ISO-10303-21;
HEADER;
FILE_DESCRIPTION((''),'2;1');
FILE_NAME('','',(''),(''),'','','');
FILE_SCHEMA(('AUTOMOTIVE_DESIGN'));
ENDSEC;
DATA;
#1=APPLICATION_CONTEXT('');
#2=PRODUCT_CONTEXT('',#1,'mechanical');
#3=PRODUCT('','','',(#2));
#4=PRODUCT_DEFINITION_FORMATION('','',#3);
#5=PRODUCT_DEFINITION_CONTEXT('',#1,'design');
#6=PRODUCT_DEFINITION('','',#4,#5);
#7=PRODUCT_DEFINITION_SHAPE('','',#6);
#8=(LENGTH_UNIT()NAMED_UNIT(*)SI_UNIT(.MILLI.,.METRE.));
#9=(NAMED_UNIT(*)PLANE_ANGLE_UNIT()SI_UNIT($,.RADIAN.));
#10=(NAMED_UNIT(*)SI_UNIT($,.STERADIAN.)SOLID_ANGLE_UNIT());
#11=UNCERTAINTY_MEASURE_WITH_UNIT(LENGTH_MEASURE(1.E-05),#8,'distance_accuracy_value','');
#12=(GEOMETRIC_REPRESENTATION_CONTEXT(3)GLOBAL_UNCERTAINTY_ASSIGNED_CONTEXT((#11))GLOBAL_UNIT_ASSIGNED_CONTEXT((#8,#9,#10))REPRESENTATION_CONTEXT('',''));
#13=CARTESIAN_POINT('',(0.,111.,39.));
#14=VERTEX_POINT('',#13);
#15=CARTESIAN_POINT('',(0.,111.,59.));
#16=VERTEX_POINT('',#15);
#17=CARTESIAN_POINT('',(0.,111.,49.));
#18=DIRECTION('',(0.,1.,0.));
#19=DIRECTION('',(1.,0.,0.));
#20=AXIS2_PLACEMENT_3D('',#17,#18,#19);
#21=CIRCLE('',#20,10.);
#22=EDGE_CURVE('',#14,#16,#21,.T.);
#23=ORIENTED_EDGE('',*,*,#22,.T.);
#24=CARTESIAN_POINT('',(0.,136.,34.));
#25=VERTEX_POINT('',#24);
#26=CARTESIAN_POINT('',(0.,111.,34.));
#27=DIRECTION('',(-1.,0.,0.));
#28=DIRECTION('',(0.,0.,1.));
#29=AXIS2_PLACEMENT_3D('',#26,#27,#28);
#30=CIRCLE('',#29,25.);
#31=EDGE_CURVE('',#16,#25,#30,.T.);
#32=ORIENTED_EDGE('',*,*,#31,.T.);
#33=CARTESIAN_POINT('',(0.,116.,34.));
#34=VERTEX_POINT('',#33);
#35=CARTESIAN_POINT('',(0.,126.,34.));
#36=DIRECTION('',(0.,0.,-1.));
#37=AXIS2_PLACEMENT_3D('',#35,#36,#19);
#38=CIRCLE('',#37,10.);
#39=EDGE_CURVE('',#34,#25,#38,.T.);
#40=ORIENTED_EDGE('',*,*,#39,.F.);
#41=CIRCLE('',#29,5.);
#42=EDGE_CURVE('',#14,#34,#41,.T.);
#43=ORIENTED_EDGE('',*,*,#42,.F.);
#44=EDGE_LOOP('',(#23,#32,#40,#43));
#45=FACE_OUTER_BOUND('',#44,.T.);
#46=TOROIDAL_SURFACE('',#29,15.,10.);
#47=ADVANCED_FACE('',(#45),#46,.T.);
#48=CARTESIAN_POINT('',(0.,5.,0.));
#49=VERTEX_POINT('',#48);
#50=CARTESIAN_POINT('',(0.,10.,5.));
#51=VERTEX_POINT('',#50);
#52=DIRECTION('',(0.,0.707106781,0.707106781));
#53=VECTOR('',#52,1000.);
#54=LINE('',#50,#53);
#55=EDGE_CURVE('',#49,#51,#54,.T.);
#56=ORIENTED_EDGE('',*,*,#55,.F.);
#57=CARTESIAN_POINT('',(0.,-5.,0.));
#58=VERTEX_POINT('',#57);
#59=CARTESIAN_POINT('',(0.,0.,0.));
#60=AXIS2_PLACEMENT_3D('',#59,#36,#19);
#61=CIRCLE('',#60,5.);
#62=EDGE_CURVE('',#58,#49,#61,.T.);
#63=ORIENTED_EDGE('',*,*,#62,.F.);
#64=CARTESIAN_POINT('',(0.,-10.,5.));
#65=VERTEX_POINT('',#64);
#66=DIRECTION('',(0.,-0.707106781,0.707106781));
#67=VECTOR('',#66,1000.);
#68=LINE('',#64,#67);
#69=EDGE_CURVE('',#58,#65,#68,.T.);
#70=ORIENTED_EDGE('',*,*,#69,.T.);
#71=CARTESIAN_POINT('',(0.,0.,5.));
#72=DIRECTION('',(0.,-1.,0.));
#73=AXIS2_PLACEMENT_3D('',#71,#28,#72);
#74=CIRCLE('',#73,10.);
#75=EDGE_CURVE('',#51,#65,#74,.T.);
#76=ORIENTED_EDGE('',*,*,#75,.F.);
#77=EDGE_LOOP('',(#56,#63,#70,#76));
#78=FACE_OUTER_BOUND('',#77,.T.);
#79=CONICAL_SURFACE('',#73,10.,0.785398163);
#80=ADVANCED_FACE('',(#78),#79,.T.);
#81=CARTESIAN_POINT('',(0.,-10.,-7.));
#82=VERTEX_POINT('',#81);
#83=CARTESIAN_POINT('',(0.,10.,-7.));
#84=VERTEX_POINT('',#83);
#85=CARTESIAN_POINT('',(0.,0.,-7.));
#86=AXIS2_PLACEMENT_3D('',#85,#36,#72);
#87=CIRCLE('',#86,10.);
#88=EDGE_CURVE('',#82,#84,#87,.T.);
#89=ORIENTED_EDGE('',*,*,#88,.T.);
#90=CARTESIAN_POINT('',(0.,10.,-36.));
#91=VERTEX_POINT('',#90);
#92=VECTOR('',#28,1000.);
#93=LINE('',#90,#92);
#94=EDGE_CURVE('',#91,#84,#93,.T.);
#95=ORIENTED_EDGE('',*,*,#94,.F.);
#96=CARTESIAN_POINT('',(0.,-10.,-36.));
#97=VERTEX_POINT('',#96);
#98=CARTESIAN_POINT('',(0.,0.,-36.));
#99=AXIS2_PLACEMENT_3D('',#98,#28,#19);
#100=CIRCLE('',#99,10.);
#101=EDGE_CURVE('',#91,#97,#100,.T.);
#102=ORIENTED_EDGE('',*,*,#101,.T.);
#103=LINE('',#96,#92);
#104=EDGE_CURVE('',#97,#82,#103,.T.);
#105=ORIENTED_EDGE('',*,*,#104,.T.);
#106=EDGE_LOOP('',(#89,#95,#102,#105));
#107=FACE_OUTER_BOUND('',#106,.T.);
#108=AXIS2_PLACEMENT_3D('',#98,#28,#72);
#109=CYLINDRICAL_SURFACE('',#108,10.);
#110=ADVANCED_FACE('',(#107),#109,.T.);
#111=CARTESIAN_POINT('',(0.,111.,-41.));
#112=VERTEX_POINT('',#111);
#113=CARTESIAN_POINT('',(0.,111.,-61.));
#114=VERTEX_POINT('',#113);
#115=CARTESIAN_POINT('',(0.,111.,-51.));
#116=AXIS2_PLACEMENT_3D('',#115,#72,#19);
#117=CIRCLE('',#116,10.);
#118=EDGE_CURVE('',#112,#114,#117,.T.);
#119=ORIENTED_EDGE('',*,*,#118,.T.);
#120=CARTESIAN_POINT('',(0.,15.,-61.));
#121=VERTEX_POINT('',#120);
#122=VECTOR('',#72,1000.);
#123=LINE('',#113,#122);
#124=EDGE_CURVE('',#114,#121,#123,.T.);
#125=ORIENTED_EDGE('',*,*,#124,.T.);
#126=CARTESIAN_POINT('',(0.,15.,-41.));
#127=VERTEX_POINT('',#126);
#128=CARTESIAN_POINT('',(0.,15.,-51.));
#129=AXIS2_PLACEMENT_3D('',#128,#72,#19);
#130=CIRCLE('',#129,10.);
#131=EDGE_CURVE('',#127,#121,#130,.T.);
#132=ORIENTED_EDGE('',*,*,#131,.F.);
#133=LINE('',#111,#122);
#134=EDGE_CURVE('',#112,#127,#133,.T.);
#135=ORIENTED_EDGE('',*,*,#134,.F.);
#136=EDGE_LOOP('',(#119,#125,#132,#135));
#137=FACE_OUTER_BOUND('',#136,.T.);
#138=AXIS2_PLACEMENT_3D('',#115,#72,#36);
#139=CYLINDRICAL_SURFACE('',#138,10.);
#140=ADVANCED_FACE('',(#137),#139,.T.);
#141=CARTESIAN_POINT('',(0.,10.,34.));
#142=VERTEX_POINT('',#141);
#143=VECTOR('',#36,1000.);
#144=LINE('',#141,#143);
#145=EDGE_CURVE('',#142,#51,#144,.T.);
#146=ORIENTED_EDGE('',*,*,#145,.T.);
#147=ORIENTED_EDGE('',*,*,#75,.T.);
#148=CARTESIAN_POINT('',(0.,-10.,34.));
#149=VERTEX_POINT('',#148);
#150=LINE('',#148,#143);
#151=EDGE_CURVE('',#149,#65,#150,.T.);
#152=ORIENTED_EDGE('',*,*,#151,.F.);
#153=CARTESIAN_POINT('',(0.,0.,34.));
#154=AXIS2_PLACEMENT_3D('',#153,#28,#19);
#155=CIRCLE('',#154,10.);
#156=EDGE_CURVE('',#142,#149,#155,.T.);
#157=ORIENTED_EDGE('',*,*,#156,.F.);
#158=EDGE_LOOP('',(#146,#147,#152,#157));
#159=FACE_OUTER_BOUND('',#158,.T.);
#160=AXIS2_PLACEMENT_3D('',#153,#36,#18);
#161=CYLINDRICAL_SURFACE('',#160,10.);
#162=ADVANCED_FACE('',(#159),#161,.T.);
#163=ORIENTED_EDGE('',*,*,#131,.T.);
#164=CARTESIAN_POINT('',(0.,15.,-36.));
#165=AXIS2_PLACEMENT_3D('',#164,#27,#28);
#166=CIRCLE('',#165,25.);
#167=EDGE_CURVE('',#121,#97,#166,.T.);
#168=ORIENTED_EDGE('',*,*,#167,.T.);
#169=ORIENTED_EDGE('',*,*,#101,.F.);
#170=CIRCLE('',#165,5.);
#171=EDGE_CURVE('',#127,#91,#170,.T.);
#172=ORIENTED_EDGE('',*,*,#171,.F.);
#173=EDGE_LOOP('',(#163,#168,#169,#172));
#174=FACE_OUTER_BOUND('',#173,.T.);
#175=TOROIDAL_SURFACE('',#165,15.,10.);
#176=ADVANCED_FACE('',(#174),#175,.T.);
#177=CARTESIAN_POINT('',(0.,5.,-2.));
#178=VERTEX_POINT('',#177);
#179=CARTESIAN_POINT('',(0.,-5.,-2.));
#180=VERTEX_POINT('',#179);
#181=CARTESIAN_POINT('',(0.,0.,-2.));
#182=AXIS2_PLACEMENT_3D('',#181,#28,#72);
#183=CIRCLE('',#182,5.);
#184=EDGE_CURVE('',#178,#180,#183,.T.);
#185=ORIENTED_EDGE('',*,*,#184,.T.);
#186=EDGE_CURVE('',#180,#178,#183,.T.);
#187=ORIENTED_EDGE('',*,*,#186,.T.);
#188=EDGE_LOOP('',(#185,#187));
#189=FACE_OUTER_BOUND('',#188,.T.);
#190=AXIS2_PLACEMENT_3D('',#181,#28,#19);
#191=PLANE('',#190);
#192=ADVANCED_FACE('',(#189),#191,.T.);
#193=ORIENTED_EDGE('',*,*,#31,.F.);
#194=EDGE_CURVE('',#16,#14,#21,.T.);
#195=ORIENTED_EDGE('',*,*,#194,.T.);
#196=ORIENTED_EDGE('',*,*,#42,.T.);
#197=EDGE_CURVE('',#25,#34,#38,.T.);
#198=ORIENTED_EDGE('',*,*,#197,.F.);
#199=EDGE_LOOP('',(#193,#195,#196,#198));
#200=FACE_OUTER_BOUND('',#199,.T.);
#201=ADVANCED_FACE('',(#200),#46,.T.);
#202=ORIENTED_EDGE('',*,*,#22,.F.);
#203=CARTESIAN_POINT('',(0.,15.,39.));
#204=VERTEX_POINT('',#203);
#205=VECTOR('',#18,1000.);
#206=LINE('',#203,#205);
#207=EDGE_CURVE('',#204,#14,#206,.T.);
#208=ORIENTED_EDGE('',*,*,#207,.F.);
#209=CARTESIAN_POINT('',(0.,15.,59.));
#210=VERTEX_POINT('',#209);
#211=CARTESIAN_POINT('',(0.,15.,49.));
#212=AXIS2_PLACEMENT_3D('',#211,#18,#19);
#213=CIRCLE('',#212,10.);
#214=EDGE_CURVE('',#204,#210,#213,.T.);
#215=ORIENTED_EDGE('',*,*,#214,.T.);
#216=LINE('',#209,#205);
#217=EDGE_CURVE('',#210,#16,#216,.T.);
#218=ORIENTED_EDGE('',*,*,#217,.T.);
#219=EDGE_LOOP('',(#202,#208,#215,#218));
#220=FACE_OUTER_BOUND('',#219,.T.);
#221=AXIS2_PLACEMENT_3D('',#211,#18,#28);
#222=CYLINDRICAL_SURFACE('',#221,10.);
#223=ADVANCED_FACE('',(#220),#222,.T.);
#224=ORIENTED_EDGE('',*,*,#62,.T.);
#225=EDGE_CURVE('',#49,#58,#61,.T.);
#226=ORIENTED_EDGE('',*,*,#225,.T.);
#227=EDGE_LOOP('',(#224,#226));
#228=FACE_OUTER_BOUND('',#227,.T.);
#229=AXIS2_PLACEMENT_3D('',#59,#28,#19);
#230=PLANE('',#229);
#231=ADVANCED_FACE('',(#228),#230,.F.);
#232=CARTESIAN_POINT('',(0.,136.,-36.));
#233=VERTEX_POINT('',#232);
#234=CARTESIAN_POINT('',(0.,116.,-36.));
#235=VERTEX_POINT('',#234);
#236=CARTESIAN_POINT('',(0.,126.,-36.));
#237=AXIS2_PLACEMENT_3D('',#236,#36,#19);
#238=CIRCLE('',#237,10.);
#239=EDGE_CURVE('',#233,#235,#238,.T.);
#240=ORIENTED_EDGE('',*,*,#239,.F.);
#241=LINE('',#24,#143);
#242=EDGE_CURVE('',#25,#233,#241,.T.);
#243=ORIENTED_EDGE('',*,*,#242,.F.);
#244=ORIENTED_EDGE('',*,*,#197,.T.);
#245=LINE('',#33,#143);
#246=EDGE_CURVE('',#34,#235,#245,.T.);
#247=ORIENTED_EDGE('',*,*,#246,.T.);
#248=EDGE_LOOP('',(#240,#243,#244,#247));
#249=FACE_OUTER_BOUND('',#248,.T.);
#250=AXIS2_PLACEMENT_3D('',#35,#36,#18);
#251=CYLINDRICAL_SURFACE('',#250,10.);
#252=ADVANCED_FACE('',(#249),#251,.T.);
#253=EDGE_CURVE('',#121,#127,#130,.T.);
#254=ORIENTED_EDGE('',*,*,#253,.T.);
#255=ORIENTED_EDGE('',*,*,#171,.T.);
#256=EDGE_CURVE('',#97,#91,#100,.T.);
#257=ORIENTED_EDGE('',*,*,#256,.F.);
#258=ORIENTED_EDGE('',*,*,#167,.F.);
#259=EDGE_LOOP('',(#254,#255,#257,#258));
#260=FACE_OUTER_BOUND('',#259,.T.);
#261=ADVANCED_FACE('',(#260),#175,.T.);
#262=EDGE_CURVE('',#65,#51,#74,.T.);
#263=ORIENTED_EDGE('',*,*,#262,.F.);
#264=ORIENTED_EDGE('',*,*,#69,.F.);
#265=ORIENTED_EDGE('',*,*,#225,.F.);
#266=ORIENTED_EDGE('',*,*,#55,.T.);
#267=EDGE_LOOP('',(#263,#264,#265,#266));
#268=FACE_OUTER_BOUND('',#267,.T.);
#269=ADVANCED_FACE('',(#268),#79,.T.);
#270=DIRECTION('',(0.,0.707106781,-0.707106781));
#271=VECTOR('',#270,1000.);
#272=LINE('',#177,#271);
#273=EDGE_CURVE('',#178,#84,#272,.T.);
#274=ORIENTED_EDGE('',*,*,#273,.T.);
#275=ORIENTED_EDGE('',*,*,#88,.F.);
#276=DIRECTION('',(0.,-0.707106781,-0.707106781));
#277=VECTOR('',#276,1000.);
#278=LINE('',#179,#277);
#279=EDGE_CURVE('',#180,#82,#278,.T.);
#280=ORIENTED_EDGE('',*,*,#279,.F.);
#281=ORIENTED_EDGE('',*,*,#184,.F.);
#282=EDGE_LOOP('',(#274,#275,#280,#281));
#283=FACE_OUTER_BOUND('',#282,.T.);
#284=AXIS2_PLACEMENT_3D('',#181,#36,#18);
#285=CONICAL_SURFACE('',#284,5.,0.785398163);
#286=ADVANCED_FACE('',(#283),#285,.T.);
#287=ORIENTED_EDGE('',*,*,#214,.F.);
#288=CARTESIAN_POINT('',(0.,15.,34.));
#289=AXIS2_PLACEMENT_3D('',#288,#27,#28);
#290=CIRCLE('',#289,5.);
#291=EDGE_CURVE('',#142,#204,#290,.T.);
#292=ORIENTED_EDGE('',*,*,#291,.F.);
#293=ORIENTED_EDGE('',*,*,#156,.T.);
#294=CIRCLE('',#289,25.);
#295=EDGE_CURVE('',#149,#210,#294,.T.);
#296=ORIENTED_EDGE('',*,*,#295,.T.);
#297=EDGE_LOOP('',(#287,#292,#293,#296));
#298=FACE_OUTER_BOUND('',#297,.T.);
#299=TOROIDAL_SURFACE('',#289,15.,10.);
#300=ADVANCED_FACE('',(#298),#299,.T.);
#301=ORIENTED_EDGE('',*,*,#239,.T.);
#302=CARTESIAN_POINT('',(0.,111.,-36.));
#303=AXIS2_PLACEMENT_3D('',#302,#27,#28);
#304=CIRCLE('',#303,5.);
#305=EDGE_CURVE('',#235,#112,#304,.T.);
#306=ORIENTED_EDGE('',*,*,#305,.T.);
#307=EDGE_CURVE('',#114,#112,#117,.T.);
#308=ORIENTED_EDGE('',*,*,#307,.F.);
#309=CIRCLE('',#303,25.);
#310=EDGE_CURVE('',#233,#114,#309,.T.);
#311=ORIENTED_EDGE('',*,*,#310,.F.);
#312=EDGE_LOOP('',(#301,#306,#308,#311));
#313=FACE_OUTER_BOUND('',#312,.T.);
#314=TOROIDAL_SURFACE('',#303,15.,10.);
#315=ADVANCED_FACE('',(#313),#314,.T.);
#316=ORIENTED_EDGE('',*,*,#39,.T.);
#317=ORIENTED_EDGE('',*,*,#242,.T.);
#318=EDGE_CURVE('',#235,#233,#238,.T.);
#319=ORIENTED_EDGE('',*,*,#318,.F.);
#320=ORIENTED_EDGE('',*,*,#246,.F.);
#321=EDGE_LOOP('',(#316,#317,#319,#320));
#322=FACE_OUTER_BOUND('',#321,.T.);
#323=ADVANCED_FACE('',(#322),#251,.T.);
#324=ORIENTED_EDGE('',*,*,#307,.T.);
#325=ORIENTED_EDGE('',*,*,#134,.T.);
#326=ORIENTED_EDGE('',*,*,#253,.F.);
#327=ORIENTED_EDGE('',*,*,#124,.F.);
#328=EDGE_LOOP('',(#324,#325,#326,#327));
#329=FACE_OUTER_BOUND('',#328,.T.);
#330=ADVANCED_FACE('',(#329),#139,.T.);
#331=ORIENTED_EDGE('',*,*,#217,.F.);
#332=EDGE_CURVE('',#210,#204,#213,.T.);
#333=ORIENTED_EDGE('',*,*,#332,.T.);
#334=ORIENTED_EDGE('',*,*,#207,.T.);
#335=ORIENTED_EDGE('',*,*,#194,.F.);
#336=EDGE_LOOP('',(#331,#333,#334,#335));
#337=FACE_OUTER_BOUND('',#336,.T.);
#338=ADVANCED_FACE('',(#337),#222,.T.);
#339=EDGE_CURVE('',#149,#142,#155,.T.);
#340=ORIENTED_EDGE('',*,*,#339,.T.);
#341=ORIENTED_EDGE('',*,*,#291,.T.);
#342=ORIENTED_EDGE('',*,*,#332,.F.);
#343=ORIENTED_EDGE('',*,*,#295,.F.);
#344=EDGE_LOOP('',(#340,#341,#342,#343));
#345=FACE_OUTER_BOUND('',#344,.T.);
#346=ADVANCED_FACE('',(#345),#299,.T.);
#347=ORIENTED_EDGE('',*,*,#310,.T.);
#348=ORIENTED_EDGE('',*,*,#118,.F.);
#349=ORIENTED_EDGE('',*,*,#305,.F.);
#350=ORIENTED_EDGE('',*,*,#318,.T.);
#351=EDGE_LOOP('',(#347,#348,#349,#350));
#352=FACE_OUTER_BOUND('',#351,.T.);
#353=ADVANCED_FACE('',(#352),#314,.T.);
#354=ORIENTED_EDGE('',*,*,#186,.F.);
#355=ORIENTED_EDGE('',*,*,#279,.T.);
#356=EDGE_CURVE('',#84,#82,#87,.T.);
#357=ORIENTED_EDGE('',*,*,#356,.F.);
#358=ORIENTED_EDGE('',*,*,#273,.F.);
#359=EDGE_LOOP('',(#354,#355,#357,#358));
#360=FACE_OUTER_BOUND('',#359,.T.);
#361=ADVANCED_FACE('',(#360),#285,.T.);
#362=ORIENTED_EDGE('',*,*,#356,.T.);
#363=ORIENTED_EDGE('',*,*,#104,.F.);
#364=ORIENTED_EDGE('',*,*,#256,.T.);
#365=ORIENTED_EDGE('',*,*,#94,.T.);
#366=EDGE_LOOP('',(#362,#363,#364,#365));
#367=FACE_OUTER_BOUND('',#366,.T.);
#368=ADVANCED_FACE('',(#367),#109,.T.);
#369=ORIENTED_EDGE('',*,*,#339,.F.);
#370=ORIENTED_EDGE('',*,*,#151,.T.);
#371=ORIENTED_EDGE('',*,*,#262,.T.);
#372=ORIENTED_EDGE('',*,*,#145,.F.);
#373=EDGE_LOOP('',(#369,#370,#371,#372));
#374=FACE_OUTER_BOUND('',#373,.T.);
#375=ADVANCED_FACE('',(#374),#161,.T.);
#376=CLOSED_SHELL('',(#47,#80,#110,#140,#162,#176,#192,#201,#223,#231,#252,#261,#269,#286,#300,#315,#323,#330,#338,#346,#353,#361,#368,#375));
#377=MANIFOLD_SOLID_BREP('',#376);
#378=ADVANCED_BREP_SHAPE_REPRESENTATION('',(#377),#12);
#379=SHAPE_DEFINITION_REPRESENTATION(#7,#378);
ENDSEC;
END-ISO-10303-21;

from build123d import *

# Parameters (mm, degrees)
SKETCH2_R     = 10
CHAMFER1_SIZE = 5


with BuildPart() as part:
    # Sweep1: sweep along a path in Sketch4
    with BuildLine(Plane(origin=(0, 0, 0), x_dir=(0, 0, -1), z_dir=(1, 0, 0))) as sweep1_path:
        Line((0, 0), (-34, 0))
        ThreePointArc((-34, 0), (-44.606601718, 4.393398282), (-49, 15))
        Line((-49, 15), (-49, 111))
        ThreePointArc((-49, 111), (-44.606601718, 121.606601718), (-34, 126))
        Line((-34, 126), (36, 126))
        ThreePointArc((36, 126), (46.606601718, 121.606601718), (51, 111))
        Line((51, 111), (51, 15))
        ThreePointArc((51, 15), (46.606601718, 4.393398282), (36, 0))
        Line((36, 0), (2, 0))
    # Sketch2 → Sweep1 (sweep)
    with BuildSketch(Plane.XY):
        Circle(SKETCH2_R)
    sweep(path=sweep1_path.line)

    # Chamfer1
    chamfer1_edges = [part.edges().sort_by_distance(p)[0] for p in [
        (-10, 0, -2),
        (-10, 0, 0),
    ]]
    chamfer(chamfer1_edges, length=CHAMFER1_SIZE)


solid = part.part
